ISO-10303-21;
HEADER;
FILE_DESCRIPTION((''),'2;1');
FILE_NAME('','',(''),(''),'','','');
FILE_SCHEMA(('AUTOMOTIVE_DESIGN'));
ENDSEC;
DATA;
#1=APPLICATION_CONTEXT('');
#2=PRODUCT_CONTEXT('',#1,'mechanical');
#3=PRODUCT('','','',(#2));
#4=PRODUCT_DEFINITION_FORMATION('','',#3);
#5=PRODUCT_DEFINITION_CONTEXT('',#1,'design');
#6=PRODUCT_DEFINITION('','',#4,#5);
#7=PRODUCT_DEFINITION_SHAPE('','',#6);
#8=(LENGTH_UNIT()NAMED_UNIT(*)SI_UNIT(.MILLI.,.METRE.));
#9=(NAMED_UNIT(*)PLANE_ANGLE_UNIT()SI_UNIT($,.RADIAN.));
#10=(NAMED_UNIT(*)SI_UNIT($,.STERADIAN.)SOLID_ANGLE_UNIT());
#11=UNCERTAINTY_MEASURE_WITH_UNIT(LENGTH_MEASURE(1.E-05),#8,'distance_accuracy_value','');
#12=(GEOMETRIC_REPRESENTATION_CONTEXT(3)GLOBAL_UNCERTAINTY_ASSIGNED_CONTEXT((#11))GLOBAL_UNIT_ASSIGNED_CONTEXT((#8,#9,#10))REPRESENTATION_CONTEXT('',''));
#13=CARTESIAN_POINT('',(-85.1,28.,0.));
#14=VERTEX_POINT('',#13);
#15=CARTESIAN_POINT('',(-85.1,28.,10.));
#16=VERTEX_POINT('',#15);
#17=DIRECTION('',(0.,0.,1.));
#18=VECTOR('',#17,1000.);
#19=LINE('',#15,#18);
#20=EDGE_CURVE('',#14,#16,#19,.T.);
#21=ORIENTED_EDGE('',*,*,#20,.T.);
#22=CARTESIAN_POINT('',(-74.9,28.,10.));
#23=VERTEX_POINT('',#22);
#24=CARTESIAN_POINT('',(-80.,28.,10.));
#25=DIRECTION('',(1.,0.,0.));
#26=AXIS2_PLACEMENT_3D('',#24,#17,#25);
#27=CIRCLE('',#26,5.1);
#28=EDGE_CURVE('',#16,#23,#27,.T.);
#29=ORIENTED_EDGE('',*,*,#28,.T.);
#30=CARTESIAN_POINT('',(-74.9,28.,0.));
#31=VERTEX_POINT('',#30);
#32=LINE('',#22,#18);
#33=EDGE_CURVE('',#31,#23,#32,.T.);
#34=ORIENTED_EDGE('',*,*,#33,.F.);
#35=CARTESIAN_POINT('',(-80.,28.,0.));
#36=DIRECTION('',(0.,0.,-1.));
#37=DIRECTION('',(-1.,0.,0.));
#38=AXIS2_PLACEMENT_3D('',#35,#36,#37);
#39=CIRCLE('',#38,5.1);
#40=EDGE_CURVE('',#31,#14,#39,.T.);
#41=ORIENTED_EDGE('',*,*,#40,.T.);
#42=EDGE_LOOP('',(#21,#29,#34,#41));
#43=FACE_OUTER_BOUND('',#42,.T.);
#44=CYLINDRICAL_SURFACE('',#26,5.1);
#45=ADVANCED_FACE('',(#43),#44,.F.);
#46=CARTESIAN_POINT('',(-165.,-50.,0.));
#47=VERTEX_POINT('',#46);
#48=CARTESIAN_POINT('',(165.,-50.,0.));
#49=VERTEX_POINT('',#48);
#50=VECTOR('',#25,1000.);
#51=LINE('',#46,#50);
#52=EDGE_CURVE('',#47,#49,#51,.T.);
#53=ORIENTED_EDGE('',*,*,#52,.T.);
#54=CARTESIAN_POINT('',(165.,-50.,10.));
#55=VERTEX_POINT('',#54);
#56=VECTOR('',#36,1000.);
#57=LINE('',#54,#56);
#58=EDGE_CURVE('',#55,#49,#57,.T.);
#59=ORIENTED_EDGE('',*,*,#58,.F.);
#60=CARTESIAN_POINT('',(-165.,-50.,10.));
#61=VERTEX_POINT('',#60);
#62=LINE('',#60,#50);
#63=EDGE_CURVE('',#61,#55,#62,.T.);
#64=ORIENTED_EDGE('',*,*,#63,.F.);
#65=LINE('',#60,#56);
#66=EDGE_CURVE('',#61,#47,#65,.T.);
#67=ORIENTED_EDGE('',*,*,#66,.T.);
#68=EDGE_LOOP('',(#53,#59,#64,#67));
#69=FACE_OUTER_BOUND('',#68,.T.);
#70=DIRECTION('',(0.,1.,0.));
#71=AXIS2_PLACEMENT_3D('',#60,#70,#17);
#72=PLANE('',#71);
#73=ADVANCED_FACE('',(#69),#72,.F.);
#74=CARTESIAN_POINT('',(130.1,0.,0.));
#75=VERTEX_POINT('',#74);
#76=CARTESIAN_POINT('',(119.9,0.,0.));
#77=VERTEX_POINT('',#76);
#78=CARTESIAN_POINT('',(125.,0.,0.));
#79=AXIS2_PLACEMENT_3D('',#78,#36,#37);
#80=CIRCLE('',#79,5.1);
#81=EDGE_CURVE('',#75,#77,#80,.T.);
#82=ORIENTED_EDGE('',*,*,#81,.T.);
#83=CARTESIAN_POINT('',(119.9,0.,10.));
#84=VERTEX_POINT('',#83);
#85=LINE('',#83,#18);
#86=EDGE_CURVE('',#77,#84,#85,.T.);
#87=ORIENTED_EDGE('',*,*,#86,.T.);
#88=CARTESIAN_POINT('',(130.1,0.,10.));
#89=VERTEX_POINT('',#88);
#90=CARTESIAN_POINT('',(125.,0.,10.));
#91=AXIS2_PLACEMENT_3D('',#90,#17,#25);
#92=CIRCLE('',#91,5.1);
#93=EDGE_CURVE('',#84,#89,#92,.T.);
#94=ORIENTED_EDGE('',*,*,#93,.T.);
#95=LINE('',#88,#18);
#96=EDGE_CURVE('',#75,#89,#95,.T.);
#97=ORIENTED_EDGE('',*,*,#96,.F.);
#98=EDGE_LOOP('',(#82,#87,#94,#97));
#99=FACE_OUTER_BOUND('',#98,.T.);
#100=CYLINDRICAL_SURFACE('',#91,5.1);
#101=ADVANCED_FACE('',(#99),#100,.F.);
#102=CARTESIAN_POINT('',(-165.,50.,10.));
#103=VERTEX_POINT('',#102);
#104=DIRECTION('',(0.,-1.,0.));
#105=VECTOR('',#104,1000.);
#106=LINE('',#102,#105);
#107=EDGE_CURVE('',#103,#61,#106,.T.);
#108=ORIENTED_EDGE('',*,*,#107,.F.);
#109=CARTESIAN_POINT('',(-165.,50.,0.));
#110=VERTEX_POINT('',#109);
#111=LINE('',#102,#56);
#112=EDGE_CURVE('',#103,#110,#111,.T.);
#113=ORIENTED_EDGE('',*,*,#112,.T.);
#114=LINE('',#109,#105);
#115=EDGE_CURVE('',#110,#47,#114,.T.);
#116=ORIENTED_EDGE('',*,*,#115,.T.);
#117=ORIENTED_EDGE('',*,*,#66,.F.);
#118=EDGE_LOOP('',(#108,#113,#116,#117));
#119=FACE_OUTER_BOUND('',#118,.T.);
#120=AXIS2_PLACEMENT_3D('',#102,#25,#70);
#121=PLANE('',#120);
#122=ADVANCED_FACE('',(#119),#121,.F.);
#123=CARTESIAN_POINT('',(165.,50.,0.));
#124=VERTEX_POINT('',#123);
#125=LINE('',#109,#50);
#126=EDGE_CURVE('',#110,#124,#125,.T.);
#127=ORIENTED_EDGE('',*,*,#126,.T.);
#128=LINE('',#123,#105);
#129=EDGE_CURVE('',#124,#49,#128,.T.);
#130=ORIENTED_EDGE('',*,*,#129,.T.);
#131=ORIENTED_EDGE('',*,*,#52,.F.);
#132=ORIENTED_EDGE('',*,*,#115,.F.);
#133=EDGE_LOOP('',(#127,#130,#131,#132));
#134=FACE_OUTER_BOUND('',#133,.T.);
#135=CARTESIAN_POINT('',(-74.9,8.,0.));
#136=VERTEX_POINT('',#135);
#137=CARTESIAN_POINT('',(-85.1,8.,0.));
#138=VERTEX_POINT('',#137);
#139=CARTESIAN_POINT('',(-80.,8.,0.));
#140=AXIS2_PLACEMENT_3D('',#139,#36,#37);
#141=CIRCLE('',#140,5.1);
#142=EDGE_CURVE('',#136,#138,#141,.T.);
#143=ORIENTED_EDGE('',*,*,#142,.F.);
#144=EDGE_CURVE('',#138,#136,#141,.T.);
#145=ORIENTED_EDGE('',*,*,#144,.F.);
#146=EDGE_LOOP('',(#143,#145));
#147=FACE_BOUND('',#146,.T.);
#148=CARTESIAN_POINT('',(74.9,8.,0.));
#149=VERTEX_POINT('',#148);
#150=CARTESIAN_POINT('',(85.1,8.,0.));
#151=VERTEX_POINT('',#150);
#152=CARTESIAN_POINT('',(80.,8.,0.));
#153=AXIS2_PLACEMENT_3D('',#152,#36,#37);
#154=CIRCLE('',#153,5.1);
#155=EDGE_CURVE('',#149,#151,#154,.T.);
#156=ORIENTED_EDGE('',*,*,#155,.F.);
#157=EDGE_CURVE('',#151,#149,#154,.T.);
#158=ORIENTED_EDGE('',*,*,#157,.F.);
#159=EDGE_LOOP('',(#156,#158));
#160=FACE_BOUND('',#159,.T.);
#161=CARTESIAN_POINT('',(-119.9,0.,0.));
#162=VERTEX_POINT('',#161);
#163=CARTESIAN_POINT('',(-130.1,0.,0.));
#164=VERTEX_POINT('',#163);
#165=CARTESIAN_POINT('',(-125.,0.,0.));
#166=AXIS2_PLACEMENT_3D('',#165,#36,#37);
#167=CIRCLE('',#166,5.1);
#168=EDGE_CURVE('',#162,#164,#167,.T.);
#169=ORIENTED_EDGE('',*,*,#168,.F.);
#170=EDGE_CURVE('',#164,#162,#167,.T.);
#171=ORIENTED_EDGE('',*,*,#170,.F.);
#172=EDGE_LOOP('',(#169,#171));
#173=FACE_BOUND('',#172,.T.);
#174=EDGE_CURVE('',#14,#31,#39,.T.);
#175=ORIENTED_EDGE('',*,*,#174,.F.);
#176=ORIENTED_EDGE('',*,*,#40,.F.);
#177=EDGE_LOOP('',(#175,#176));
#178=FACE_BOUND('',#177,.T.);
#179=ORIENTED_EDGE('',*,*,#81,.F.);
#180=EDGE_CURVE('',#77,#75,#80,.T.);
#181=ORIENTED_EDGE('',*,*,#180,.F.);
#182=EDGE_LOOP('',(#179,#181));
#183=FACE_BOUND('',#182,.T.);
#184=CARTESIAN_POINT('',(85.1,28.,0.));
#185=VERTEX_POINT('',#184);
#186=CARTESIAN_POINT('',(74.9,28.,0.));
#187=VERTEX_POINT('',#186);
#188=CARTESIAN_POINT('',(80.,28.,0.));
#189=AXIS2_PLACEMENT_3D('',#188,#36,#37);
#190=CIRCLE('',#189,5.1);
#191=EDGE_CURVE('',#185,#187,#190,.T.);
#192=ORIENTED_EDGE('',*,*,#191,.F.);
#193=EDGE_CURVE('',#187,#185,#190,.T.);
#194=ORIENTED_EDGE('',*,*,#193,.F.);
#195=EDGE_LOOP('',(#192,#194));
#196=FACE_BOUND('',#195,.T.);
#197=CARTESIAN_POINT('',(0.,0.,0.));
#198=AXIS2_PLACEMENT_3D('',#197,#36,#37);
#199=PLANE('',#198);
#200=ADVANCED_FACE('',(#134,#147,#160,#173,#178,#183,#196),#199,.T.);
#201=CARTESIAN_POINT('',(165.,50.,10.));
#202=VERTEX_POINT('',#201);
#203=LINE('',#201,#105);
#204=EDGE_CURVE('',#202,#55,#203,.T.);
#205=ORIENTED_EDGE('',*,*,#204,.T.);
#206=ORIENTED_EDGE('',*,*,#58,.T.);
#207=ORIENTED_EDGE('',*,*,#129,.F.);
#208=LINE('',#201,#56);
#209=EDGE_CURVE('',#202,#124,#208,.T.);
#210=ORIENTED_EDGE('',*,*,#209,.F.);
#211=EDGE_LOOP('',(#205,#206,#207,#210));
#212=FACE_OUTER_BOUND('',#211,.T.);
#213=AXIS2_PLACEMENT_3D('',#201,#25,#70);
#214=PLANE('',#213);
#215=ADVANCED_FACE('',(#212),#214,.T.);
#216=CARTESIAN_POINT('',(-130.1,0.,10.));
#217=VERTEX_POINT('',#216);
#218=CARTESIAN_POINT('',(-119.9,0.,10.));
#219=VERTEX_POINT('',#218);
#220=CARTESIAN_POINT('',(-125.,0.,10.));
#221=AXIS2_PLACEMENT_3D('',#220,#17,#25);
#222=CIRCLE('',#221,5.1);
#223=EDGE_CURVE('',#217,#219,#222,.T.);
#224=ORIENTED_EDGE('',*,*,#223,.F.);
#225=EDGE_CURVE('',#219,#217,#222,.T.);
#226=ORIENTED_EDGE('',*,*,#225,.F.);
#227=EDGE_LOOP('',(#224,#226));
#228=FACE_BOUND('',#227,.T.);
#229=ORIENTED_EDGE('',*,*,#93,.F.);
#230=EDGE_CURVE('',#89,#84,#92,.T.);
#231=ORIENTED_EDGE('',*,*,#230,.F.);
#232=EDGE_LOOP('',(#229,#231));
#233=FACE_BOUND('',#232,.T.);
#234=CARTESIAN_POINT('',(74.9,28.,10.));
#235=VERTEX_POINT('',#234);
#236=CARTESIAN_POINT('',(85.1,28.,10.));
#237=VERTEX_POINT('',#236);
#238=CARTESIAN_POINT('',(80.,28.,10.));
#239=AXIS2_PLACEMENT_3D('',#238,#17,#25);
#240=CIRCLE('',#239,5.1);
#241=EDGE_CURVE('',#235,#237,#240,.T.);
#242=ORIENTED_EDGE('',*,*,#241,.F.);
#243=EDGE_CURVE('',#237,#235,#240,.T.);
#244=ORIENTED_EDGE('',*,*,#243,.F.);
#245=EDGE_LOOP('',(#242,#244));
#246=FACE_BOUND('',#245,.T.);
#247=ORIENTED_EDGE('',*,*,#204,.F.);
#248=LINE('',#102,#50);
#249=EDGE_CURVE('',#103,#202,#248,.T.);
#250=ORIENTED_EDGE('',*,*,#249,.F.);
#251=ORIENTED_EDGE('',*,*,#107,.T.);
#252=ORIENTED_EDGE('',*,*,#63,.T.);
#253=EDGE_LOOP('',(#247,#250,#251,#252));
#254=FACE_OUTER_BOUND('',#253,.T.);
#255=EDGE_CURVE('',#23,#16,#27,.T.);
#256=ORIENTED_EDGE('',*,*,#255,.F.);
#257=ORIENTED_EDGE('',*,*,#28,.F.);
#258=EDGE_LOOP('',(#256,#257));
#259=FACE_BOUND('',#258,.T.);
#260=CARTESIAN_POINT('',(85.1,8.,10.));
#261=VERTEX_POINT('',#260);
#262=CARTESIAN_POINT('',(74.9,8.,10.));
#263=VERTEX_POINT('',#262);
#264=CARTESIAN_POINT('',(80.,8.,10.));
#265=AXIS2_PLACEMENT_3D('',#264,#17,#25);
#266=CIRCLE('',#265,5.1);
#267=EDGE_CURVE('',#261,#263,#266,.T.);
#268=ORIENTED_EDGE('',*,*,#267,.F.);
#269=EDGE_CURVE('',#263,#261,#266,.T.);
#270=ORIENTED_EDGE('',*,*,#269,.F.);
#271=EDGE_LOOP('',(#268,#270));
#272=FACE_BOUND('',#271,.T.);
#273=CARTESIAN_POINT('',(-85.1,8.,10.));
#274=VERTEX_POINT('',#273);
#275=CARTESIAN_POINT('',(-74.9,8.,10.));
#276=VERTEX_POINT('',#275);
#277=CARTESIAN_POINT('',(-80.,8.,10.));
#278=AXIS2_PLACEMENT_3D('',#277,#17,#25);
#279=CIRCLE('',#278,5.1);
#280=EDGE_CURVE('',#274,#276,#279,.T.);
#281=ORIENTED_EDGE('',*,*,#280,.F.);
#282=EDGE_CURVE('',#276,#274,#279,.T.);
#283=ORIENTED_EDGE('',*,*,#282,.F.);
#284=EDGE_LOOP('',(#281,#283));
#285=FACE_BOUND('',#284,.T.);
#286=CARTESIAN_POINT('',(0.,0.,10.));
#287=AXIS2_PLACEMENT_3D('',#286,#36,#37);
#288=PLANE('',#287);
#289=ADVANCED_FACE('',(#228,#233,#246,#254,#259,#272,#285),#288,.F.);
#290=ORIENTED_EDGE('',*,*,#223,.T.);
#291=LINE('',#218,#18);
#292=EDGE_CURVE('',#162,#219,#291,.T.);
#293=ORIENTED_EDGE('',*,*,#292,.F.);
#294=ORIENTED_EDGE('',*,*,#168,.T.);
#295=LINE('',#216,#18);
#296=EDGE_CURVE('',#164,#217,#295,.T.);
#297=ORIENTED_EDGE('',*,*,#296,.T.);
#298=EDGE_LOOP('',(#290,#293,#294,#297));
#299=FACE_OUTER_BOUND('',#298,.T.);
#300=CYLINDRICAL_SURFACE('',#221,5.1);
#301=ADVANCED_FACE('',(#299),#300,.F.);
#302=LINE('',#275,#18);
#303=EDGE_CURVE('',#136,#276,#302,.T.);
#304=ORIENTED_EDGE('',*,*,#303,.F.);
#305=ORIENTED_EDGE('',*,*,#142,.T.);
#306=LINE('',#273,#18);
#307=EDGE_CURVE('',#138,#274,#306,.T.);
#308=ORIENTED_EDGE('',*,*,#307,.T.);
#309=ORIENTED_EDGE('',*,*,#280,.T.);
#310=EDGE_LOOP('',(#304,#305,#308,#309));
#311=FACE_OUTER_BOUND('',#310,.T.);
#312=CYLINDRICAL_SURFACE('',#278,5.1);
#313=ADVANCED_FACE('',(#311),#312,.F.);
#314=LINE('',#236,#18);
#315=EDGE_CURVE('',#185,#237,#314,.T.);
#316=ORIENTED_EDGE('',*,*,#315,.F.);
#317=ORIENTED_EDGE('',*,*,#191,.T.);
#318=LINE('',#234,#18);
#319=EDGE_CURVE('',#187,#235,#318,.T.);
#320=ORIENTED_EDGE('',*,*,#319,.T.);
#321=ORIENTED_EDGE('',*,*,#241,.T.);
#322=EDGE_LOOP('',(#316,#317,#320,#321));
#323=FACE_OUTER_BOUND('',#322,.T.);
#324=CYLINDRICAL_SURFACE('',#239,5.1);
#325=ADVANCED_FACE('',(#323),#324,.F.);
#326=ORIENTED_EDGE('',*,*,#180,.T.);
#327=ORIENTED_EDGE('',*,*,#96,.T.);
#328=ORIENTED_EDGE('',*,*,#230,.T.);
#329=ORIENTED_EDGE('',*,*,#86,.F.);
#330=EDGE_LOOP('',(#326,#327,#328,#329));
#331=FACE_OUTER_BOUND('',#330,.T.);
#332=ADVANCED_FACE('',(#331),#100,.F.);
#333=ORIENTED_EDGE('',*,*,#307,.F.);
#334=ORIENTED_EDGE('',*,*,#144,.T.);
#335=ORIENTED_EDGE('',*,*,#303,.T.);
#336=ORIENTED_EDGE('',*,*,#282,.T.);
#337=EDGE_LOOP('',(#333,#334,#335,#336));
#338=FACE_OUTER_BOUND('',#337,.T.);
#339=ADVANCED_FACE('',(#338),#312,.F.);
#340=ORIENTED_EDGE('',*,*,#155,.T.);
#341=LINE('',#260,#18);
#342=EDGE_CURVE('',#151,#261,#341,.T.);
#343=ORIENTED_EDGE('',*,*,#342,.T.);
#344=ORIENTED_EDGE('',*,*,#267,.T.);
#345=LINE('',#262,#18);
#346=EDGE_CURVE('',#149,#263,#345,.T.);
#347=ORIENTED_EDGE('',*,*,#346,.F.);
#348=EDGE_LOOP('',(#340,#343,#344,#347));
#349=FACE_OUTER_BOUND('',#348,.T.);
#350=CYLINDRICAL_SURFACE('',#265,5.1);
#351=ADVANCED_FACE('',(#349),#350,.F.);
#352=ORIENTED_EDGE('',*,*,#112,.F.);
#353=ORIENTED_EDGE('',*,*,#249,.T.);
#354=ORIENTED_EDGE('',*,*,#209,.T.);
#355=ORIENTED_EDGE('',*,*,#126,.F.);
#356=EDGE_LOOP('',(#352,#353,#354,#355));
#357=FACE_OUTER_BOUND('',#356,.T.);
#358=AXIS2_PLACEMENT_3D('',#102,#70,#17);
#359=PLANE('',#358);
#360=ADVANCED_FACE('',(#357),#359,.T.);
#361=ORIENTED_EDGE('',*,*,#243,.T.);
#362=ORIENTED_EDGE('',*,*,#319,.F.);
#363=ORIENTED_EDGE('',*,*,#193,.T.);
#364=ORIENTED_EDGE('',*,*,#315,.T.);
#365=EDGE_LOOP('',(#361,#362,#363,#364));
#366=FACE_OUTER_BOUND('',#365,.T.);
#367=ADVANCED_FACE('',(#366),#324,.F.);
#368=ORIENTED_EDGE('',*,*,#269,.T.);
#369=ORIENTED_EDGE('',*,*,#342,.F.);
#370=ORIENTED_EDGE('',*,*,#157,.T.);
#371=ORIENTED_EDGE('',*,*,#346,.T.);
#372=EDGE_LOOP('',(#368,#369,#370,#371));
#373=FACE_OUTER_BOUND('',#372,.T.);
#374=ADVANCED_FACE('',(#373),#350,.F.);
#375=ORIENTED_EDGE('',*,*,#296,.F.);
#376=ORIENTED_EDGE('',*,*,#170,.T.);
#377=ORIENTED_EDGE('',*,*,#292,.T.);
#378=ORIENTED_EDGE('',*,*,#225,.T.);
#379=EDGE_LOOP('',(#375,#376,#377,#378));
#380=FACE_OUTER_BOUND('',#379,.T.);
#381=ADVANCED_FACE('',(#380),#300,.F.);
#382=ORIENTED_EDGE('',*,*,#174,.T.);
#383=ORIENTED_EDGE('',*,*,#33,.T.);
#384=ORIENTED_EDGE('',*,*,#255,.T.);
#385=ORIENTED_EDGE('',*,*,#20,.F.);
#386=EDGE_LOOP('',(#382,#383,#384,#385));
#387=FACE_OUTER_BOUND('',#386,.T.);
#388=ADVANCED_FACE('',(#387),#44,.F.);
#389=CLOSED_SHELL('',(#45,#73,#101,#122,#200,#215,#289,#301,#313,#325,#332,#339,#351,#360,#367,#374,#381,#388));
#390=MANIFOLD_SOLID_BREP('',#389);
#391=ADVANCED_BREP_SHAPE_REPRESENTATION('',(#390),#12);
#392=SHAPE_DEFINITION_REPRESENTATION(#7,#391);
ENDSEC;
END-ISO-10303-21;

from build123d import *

# Parameters (mm, degrees)
SKETCH1_W              = 330
SKETCH1_H              = 100
BOSS_EXTRUDE1_DEPTH    = 10
M12_TAPPED_HOLE1_D     = 10.2
M12_TAPPED_HOLE1_DEPTH = 29.25
M12_TAPPED_HOLE1_TIP   = 3.064389157


with BuildPart() as part:
    # Sketch1 → Boss-Extrude1 (new body)
    with BuildSketch(Plane.XY):
        Rectangle(SKETCH1_W, SKETCH1_H)
    extrude(amount=BOSS_EXTRUDE1_DEPTH)

    # M12 Tapped Hole1
    with Locations(Plane.XY.offset(10)):
        with Locations((-125, 0), (-80, 8), (-80, 28), (80, 28), (80, 8), (125, 0)):
            Hole(M12_TAPPED_HOLE1_D / 2, depth=M12_TAPPED_HOLE1_DEPTH)
            with Locations((0, 0, -(M12_TAPPED_HOLE1_DEPTH + M12_TAPPED_HOLE1_TIP / 2))):  # 118° drill point
                Cone(0, M12_TAPPED_HOLE1_D / 2, M12_TAPPED_HOLE1_TIP, mode=Mode.SUBTRACT)


solid = part.part
